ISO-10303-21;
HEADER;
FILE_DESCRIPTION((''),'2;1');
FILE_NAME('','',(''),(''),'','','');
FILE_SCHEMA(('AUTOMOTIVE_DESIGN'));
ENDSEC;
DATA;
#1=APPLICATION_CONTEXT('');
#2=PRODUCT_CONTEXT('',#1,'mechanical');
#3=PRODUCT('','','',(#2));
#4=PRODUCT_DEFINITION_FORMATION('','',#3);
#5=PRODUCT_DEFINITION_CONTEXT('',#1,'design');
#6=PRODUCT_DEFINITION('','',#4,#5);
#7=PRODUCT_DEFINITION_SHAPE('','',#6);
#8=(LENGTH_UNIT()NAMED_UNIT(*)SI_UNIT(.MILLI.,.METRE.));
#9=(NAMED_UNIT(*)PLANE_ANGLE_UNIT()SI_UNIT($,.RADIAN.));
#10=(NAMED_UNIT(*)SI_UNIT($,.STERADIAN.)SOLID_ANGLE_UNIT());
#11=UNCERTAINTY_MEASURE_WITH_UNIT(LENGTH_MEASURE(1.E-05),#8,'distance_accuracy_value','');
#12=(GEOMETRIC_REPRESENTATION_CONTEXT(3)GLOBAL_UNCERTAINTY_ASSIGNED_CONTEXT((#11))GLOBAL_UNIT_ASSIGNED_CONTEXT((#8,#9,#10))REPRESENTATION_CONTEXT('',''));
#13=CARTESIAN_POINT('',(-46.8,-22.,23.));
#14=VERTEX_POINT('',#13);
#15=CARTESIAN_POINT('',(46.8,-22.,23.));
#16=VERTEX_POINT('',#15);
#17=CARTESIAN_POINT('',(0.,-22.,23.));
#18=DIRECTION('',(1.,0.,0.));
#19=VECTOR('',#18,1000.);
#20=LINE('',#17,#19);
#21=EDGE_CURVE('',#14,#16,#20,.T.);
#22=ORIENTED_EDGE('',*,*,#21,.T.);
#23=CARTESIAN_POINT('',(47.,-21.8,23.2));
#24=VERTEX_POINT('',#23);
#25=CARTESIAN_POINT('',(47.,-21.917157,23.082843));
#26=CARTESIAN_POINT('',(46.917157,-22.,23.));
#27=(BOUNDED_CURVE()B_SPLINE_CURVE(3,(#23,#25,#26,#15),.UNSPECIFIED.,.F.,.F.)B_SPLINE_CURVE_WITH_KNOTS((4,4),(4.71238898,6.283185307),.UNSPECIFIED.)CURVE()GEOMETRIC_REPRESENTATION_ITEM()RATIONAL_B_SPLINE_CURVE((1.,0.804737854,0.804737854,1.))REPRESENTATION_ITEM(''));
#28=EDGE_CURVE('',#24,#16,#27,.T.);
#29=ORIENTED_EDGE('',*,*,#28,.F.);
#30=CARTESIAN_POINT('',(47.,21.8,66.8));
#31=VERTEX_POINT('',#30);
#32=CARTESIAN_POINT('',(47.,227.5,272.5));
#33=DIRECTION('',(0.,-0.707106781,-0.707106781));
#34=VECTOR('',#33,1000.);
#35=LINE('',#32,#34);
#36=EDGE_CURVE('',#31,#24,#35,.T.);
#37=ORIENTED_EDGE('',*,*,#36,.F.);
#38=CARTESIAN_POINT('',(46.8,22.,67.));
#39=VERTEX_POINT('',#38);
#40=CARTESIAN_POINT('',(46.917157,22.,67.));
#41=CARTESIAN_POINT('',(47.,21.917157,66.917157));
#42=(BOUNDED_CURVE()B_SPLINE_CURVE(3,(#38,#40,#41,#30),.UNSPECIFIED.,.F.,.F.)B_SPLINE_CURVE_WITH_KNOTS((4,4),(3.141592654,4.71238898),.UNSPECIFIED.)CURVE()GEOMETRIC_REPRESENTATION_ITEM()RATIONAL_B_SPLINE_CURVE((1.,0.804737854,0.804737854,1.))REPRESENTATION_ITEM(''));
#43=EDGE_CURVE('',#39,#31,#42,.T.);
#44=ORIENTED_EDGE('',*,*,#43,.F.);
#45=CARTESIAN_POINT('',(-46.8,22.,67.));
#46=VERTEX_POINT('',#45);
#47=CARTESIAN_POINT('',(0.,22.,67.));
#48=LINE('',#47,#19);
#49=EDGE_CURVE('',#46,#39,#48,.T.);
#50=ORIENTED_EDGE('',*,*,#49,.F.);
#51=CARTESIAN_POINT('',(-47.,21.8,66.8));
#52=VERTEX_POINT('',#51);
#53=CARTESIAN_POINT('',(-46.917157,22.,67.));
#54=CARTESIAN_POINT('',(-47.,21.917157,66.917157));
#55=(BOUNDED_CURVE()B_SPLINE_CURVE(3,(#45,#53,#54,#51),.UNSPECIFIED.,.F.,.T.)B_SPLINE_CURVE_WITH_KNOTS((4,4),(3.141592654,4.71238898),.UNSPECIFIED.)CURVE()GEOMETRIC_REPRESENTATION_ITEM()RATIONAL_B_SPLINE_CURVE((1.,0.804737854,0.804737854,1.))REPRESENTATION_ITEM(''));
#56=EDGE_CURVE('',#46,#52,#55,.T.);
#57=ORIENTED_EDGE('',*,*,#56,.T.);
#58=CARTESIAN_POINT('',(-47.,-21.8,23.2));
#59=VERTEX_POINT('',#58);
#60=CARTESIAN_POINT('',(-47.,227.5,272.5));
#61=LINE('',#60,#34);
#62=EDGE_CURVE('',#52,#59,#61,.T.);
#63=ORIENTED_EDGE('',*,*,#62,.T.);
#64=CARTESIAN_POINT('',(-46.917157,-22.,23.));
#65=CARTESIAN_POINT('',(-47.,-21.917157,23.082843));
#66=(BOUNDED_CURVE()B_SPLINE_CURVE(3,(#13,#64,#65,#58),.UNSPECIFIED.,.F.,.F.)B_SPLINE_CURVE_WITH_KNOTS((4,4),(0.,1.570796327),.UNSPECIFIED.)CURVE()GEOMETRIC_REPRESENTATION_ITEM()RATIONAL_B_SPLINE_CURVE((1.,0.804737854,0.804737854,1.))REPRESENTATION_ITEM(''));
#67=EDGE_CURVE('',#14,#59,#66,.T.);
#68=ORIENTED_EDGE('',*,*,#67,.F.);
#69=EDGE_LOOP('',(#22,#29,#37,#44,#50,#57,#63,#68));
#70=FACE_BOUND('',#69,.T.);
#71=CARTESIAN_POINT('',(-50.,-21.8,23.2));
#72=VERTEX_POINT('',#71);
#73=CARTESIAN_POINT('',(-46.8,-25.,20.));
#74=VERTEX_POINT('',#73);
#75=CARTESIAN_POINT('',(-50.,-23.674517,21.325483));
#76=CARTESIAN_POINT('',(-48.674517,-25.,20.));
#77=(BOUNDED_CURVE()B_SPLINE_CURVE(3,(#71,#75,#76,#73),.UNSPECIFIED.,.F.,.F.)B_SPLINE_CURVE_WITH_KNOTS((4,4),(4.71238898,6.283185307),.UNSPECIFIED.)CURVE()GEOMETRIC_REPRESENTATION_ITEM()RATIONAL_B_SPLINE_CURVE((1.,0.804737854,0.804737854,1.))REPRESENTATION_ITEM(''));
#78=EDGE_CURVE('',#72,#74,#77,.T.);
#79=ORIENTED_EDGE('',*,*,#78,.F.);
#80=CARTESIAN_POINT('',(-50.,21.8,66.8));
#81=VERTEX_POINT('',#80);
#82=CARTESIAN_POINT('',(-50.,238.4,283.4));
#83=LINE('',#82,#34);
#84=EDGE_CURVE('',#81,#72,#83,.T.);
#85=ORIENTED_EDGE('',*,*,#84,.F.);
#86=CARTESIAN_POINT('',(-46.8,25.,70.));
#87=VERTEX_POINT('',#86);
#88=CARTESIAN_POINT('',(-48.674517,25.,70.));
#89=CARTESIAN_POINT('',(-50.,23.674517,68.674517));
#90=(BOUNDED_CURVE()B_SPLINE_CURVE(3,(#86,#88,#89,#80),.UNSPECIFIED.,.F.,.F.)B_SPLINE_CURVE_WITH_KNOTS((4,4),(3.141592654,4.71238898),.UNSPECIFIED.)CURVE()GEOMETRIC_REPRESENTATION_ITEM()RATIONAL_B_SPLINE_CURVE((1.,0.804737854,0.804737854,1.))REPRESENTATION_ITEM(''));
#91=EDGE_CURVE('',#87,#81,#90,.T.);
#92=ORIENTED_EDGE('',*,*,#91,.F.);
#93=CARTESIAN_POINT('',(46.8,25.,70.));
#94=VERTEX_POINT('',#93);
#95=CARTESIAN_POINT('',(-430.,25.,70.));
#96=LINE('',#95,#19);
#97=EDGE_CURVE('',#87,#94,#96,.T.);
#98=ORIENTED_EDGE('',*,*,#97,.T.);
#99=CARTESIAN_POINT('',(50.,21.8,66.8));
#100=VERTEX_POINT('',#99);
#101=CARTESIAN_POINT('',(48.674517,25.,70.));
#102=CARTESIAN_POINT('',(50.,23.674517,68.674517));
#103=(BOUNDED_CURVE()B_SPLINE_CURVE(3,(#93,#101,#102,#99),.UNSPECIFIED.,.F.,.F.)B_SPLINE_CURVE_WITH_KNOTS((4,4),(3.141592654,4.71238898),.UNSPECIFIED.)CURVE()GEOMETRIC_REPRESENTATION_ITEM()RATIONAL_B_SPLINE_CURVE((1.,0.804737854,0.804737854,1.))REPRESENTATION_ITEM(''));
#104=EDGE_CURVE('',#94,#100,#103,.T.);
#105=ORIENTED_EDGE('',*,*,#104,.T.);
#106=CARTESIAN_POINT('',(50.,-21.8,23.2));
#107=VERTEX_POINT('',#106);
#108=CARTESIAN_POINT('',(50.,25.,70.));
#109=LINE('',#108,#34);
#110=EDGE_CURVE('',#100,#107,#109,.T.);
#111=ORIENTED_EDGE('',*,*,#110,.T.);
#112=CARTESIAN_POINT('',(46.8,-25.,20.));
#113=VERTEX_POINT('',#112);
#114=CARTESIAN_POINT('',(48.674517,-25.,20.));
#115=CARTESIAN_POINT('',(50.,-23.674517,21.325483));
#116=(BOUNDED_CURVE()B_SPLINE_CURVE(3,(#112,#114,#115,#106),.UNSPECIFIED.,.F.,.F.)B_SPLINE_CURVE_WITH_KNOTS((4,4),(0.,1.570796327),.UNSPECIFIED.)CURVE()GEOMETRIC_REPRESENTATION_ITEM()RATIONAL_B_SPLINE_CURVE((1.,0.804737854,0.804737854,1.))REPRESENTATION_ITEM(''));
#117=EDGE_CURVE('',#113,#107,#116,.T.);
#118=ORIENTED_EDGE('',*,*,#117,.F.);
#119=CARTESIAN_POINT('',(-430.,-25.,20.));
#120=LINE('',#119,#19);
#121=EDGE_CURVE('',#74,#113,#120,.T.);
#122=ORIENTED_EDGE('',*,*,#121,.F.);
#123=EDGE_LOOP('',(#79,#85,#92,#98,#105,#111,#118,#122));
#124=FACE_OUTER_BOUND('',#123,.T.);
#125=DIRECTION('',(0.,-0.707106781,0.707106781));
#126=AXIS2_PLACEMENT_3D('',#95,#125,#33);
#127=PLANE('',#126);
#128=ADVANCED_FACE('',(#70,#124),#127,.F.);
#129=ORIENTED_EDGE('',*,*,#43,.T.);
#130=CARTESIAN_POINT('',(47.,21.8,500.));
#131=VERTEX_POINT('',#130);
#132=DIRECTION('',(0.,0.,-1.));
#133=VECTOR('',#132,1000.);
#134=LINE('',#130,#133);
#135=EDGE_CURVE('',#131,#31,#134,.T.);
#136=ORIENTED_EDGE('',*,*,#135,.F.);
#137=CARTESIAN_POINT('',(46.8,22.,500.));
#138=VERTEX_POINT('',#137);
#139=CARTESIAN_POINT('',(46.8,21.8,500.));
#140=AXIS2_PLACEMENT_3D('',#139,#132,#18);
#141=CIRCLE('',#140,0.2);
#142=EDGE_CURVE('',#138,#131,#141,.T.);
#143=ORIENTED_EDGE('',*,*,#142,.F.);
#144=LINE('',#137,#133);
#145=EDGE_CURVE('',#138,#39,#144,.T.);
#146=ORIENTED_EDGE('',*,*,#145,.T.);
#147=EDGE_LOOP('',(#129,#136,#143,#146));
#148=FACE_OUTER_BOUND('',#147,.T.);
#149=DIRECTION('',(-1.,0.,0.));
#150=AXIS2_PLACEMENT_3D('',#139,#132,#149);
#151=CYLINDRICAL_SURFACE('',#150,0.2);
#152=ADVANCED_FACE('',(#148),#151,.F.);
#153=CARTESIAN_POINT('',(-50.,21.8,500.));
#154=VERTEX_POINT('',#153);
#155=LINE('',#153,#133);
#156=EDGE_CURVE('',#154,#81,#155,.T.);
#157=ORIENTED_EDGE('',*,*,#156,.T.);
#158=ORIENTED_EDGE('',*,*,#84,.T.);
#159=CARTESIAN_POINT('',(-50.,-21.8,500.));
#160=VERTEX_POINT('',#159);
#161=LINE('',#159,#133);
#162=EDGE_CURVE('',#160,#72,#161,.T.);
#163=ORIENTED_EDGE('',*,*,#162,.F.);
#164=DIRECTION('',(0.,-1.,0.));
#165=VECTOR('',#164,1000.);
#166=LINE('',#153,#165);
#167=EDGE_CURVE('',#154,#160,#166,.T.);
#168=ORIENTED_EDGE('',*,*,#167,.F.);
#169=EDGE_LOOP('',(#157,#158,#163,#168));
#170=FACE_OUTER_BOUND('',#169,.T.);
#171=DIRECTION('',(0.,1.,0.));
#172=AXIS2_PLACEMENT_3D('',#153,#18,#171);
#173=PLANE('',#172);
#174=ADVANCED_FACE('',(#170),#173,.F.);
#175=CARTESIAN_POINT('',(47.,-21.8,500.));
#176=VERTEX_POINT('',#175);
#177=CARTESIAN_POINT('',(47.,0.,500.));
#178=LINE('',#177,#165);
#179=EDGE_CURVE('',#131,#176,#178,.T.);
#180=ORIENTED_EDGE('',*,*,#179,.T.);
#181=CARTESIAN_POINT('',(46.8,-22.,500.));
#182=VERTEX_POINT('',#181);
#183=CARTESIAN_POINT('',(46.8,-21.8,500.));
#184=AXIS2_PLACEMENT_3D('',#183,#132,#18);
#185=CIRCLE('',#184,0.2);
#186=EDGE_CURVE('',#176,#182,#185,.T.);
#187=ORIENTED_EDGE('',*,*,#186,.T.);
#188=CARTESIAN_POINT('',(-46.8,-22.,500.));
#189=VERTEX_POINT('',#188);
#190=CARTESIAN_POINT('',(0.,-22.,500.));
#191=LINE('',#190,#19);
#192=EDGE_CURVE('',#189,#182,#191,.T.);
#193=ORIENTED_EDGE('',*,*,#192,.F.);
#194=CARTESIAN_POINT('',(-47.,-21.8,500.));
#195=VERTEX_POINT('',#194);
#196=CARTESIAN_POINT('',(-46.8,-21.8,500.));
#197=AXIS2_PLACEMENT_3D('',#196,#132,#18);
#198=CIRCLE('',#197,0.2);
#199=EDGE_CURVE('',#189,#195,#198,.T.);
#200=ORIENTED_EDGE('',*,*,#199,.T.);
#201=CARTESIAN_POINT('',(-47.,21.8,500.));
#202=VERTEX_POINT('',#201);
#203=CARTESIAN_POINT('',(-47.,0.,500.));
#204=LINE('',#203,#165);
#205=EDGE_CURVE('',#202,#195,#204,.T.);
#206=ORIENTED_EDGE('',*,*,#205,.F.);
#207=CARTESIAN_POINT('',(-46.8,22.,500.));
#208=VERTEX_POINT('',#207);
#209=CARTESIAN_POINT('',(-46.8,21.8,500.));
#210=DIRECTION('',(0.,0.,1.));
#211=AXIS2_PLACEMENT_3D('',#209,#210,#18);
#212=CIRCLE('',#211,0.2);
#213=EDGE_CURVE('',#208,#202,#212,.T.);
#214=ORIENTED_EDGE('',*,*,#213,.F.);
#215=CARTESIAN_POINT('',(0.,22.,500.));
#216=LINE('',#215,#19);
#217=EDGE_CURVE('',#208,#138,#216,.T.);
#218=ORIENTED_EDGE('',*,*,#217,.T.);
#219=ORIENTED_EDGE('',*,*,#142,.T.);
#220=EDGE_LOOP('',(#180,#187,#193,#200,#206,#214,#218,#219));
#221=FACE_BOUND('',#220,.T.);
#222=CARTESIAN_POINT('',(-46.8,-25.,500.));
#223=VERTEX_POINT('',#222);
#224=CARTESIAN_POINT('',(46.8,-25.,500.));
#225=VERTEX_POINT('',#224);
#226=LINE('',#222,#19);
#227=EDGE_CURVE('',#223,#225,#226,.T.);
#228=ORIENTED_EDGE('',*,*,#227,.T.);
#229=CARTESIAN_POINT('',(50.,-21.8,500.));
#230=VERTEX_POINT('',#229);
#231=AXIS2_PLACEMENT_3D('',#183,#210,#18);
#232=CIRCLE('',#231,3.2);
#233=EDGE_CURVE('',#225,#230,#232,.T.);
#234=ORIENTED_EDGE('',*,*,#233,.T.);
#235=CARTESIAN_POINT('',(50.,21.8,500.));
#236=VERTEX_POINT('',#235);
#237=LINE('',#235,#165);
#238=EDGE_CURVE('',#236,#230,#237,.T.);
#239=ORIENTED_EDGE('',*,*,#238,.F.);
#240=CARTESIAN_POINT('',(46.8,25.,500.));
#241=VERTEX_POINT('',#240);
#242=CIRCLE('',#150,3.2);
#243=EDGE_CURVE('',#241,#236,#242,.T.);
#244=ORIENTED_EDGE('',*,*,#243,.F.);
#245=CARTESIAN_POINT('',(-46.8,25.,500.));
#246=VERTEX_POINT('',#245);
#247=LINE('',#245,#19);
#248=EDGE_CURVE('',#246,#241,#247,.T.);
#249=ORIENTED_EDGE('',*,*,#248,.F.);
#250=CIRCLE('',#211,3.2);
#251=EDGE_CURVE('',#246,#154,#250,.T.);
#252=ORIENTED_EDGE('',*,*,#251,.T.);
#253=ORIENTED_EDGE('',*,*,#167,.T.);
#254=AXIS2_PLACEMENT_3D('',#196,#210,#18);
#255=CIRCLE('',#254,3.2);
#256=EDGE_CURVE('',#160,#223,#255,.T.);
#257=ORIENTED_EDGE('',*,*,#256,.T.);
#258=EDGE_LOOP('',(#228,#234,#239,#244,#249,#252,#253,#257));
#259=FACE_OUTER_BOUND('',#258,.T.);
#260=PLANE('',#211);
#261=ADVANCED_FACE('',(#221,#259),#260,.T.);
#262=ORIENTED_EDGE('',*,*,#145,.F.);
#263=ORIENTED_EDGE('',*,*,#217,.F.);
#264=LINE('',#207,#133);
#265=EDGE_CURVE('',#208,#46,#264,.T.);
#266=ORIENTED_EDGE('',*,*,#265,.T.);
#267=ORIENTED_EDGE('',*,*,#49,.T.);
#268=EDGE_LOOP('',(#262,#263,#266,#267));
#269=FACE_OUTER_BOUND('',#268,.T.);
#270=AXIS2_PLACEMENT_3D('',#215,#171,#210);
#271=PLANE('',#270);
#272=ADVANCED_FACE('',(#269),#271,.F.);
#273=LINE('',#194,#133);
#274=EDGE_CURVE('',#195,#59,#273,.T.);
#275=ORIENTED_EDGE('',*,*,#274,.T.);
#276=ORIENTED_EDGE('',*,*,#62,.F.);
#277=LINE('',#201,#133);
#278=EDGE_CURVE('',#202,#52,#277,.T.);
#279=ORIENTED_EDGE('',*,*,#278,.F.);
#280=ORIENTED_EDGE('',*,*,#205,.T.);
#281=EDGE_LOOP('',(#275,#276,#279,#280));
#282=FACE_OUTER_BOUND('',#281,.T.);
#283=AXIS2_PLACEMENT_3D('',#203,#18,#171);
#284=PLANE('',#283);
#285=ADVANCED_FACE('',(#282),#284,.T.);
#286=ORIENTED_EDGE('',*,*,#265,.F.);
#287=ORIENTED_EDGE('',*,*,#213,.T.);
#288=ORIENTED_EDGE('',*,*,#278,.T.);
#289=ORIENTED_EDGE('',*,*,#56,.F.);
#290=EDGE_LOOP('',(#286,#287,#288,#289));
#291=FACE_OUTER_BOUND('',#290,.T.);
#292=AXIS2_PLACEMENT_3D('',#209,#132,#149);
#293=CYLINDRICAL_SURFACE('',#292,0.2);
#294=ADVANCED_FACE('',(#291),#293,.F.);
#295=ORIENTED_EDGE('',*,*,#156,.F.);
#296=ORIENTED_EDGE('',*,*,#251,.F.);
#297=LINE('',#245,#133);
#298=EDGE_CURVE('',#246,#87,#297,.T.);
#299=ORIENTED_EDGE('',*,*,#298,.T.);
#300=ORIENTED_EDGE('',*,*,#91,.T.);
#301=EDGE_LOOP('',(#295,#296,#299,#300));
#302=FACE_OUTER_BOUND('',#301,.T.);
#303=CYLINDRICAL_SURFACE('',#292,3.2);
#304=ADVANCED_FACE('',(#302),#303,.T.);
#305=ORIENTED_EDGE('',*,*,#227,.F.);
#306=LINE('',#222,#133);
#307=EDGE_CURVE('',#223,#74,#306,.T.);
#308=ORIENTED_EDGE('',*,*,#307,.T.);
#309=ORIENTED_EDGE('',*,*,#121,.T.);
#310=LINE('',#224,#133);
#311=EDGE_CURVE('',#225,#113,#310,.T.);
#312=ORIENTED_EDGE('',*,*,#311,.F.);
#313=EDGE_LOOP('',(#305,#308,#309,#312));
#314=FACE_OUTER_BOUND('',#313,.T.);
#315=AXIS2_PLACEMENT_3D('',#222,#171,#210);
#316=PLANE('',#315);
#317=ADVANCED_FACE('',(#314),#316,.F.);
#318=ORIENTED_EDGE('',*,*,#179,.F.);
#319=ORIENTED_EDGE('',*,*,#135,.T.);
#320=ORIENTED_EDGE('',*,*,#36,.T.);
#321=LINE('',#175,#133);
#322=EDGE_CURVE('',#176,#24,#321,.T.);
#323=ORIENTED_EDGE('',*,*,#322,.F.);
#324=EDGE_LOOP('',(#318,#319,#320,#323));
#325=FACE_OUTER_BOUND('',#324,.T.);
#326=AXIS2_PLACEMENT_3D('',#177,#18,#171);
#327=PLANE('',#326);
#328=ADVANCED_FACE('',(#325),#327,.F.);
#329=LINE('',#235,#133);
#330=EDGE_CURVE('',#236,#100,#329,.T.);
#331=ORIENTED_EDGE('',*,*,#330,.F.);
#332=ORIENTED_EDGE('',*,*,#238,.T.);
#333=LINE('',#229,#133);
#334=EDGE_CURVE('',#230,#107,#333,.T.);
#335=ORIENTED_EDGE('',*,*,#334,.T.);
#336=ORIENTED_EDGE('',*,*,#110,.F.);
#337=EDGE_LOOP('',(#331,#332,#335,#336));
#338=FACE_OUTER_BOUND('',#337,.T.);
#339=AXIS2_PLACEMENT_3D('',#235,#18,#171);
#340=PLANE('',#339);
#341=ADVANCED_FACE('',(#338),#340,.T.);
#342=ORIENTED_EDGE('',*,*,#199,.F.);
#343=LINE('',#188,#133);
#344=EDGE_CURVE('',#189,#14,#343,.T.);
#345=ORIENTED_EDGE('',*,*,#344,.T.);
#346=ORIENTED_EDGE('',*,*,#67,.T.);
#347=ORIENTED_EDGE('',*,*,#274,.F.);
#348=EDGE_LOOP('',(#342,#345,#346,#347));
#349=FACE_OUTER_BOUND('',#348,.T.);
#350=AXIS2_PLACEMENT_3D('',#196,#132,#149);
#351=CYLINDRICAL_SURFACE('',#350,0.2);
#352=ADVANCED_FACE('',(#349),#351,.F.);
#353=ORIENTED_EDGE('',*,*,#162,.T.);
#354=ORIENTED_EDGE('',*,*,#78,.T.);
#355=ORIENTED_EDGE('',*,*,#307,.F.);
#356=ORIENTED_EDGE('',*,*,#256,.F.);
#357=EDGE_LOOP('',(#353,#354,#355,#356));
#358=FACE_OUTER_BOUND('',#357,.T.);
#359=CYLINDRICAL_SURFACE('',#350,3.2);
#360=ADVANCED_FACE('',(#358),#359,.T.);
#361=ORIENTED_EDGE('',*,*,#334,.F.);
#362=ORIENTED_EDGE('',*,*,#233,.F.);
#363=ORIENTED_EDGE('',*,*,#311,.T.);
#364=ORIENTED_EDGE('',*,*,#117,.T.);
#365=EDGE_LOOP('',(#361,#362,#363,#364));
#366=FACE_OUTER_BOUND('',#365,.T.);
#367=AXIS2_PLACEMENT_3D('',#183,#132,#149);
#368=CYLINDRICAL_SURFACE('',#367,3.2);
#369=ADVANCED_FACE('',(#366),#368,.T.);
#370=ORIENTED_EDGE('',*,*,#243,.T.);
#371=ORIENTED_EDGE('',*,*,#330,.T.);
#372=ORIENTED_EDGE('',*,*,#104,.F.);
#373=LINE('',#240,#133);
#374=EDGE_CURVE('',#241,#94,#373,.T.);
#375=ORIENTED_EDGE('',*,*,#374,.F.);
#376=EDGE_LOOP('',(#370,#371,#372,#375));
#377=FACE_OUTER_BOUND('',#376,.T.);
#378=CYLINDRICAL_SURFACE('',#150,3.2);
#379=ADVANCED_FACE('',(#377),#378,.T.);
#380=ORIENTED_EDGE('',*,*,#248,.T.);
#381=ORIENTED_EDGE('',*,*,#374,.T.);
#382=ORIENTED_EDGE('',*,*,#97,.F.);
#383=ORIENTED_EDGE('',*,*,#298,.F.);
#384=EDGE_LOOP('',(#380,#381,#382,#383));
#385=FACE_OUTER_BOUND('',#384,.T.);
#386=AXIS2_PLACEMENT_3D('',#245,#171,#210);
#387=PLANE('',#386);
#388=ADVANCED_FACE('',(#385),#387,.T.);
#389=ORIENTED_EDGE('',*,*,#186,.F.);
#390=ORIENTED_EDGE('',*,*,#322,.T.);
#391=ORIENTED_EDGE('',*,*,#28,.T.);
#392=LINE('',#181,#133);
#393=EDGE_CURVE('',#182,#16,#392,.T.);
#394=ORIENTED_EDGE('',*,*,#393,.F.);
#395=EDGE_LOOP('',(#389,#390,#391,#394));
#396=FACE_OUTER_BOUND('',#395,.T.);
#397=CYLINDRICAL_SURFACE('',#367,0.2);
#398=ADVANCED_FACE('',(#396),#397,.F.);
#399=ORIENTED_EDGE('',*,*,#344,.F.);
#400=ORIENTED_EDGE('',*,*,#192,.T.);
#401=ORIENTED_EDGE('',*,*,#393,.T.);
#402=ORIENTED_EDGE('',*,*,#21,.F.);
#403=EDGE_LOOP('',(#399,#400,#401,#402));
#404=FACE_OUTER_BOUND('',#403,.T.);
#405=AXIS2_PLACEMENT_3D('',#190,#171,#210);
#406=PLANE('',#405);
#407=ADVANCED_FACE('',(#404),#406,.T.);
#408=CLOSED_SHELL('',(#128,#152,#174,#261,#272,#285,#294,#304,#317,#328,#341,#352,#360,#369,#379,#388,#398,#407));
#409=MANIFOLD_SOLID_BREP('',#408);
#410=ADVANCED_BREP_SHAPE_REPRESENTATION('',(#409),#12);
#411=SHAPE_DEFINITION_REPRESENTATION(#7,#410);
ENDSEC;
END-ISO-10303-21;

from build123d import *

# Parameters (mm, degrees)
EXTRUDE_1_DEPTH     = 500
CUT_EXTRUDE_1_DEPTH = 480


with BuildPart() as part:
    # 草图1 → 凸台-拉伸1 (new body)
    with BuildSketch(Plane.XY):
        with BuildLine():
            Line((-46.8, 25), (46.8, 25))
            ThreePointArc((46.8, 25), (49.0627417, 24.0627417), (50, 21.8))
            Line((50, 21.8), (50, -21.8))
            ThreePointArc((50, -21.8), (49.0627417, -24.0627417), (46.8, -25))
            Line((46.8, -25), (-46.8, -25))
            ThreePointArc((-46.8, -25), (-49.0627417, -24.0627417), (-50, -21.8))
            Line((-50, -21.8), (-50, 21.8))
            ThreePointArc((-50, 21.8), (-49.0627417, 24.0627417), (-46.8, 25))
        make_face()
        with BuildLine():
            Line((-46.8, 22), (46.8, 22))
            ThreePointArc((46.8, 22), (46.941421356, 21.941421356), (47, 21.8))
            Line((47, 21.8), (47, -21.8))
            ThreePointArc((47, -21.8), (46.941421356, -21.941421356), (46.8, -22))
            Line((46.8, -22), (-46.8, -22))
            ThreePointArc((-46.8, -22), (-46.941421356, -21.941421356), (-47, -21.8))
            Line((-47, -21.8), (-47, 21.8))
            ThreePointArc((-47, 21.8), (-46.941421356, 21.941421356), (-46.8, 22))
        make_face(mode=Mode.SUBTRACT)
    extrude(amount=EXTRUDE_1_DEPTH)

    # 草图3 → 切除-拉伸1 (cut)
    with BuildSketch(Plane(origin=(50, 0, 0), x_dir=(0, 0, -1), z_dir=(1, 0, 0))):
        Polygon((-70, 25), (-20, -25), (18.010342751, -26.423264748), (18.010342751, 25), align=None)
    extrude(amount=-CUT_EXTRUDE_1_DEPTH, mode=Mode.SUBTRACT)


solid = part.part
